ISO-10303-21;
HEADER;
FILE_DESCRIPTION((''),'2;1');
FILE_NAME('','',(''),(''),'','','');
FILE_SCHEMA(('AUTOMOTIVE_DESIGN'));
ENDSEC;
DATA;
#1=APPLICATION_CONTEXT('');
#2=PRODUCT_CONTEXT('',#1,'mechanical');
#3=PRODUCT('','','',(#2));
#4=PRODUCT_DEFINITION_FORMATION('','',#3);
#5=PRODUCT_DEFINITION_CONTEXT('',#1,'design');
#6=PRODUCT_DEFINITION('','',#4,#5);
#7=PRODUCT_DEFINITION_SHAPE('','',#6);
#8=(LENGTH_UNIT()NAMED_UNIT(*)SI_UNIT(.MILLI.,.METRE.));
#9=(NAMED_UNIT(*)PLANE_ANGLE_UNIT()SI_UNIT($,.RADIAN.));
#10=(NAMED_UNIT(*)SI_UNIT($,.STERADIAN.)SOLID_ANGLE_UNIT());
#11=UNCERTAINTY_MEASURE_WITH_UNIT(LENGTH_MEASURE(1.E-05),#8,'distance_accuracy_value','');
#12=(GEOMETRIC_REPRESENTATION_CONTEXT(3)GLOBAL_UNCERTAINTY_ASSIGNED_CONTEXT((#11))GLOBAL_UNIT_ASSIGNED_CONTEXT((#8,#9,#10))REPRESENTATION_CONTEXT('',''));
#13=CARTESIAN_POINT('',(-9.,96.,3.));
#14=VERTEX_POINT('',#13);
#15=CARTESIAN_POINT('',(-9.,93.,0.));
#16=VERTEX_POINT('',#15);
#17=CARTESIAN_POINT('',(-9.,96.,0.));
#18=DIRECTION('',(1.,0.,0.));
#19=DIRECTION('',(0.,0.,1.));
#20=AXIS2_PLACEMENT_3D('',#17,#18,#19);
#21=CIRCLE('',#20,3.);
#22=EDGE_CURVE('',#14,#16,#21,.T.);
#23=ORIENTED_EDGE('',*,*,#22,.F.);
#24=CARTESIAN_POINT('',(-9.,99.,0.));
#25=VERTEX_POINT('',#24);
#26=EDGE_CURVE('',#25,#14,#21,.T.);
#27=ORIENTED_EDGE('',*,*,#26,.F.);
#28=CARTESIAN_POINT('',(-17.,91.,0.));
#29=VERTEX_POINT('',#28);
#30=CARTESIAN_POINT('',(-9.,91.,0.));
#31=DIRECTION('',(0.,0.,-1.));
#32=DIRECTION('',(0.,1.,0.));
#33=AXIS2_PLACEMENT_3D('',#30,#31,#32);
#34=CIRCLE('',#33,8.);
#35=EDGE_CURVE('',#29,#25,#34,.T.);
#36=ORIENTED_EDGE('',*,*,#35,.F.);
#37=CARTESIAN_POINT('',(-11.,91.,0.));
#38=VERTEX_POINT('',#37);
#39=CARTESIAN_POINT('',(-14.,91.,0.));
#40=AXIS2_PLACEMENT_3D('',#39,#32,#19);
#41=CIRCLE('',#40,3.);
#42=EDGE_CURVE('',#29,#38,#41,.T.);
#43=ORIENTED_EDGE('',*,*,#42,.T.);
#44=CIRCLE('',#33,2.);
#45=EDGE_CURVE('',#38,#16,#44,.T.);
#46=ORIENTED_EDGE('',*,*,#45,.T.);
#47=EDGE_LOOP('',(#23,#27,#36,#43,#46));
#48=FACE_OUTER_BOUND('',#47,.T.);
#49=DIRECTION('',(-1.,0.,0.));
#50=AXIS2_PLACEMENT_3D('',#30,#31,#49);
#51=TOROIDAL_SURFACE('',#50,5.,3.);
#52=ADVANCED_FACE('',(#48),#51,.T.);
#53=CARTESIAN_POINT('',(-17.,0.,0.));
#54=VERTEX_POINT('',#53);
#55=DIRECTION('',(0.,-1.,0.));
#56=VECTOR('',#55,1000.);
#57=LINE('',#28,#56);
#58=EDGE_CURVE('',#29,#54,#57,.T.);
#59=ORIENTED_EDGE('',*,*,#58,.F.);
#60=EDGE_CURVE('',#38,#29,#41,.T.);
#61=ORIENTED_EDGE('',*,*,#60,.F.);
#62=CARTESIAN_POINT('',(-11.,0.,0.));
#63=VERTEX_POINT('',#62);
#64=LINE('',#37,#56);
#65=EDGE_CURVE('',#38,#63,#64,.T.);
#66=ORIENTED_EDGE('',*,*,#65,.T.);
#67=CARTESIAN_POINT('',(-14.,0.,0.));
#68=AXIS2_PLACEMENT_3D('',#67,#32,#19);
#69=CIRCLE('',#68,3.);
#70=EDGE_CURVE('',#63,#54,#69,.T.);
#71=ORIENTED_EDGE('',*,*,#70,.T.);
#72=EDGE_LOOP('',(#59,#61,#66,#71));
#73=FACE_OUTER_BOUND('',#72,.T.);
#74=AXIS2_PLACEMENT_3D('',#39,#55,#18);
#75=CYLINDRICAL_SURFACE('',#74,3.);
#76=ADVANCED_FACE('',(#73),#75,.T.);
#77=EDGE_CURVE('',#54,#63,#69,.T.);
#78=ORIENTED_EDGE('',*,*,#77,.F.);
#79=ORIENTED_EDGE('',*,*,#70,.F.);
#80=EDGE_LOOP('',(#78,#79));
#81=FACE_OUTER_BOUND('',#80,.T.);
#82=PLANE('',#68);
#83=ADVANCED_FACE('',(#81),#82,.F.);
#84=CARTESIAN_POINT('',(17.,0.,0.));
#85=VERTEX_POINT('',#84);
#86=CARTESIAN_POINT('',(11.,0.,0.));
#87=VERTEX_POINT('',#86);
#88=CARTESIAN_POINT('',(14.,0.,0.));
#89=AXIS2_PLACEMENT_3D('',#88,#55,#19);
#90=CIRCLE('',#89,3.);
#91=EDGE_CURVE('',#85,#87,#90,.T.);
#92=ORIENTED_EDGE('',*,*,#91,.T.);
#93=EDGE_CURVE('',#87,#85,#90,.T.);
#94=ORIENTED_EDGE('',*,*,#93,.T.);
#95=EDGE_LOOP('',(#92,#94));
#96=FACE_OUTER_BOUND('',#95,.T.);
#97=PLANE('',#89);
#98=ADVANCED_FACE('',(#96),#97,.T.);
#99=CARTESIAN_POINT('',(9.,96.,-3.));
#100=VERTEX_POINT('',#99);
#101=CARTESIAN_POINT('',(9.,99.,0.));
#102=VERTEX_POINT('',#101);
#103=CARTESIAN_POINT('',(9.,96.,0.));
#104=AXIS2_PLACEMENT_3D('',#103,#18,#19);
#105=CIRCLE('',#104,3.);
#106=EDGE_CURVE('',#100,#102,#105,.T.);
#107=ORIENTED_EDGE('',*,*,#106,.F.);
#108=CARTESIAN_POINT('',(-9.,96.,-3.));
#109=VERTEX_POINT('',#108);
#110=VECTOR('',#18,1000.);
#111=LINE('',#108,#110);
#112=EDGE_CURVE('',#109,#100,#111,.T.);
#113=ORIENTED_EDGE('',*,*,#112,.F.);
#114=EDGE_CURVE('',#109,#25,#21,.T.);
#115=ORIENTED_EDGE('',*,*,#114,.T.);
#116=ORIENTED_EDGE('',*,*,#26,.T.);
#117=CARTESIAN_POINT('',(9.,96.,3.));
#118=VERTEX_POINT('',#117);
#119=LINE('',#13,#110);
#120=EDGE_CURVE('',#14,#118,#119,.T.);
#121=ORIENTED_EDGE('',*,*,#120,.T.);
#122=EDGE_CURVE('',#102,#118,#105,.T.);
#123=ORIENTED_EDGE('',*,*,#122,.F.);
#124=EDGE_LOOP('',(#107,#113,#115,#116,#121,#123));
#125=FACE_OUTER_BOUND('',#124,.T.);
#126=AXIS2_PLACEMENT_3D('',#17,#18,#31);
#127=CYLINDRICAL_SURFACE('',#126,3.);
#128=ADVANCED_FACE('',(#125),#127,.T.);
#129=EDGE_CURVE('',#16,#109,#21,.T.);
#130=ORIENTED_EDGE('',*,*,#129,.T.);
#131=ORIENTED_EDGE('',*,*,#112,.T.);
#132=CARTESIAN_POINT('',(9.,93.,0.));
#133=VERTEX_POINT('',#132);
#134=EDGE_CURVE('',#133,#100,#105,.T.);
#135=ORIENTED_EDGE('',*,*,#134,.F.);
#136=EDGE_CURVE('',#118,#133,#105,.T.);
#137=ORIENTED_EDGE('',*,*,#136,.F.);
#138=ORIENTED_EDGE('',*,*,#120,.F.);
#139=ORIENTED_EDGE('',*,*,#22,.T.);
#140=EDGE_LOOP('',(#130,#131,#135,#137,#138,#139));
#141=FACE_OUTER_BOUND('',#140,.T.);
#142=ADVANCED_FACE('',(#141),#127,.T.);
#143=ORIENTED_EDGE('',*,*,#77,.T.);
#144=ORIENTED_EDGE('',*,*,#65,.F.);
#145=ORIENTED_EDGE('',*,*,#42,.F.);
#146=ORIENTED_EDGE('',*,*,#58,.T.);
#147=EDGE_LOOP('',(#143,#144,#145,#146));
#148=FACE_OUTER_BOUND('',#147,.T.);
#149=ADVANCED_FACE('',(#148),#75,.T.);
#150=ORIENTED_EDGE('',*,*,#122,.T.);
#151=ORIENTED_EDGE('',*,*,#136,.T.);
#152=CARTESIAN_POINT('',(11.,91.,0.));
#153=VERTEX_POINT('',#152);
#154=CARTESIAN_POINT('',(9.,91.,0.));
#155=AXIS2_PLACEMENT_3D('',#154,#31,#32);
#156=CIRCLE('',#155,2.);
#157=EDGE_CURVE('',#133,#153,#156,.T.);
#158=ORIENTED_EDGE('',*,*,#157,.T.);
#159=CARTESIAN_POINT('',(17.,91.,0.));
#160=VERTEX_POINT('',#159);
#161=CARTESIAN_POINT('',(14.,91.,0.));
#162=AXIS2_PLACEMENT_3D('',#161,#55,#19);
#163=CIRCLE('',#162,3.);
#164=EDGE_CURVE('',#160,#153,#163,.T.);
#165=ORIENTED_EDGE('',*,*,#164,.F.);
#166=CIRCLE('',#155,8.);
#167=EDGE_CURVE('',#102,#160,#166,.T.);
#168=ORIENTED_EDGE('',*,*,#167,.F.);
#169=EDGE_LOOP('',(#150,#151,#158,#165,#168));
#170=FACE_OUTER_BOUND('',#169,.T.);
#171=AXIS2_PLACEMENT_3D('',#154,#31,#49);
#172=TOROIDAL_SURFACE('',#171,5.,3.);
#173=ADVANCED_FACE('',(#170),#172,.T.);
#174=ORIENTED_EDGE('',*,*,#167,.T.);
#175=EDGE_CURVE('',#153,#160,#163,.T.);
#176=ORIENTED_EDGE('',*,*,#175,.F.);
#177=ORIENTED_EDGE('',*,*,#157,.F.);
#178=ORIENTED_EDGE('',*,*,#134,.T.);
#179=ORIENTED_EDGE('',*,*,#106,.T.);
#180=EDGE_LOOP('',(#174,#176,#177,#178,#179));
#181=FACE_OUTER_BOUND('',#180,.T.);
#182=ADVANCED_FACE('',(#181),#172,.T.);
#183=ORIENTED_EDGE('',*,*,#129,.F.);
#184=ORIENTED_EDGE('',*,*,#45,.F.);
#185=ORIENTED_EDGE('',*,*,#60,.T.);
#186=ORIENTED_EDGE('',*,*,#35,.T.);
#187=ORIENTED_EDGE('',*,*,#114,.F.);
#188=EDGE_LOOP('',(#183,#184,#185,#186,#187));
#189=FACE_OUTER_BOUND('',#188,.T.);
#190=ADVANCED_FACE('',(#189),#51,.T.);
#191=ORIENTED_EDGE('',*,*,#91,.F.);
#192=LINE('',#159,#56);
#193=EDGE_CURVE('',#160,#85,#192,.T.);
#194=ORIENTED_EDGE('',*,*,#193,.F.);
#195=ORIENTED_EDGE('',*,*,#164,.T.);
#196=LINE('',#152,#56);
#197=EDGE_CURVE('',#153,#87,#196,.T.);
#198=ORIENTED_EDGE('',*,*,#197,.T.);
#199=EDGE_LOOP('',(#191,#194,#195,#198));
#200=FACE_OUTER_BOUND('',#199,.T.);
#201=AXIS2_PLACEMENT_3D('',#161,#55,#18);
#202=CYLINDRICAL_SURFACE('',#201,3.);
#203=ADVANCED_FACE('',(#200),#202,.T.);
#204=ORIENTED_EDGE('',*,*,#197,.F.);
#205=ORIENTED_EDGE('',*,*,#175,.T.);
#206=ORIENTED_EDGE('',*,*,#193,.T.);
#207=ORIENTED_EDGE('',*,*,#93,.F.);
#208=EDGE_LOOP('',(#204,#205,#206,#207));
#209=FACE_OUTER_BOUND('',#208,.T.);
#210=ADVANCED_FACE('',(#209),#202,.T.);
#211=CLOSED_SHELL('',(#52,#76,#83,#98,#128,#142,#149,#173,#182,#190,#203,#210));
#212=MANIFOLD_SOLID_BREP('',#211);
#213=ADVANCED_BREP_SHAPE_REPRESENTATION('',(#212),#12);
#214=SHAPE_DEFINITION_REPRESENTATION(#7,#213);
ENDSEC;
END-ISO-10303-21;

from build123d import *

# Parameters (mm, degrees)
SKETCH_2_R = 3


with BuildPart() as part:
    # 扫描1: sweep along a path in 草图1
    with BuildLine(Plane.XY) as sweep_1_path:
        Line((-14, 0), (-14, 91))
        ThreePointArc((-14, 91), (-12.535533906, 94.535533906), (-9, 96))
        Line((-9, 96), (9, 96))
        ThreePointArc((9, 96), (12.535533906, 94.535533906), (14, 91))
        Line((14, 91), (14, 0))
    # 草图2 → 扫描1 (sweep)
    with BuildSketch(Plane(origin=(0, 0, 0), x_dir=(1, 0, 0), z_dir=(0, 1, 0))):
        with Locations((-14, 0)):
            Circle(SKETCH_2_R)
    sweep(path=sweep_1_path.line)


solid = part.part
